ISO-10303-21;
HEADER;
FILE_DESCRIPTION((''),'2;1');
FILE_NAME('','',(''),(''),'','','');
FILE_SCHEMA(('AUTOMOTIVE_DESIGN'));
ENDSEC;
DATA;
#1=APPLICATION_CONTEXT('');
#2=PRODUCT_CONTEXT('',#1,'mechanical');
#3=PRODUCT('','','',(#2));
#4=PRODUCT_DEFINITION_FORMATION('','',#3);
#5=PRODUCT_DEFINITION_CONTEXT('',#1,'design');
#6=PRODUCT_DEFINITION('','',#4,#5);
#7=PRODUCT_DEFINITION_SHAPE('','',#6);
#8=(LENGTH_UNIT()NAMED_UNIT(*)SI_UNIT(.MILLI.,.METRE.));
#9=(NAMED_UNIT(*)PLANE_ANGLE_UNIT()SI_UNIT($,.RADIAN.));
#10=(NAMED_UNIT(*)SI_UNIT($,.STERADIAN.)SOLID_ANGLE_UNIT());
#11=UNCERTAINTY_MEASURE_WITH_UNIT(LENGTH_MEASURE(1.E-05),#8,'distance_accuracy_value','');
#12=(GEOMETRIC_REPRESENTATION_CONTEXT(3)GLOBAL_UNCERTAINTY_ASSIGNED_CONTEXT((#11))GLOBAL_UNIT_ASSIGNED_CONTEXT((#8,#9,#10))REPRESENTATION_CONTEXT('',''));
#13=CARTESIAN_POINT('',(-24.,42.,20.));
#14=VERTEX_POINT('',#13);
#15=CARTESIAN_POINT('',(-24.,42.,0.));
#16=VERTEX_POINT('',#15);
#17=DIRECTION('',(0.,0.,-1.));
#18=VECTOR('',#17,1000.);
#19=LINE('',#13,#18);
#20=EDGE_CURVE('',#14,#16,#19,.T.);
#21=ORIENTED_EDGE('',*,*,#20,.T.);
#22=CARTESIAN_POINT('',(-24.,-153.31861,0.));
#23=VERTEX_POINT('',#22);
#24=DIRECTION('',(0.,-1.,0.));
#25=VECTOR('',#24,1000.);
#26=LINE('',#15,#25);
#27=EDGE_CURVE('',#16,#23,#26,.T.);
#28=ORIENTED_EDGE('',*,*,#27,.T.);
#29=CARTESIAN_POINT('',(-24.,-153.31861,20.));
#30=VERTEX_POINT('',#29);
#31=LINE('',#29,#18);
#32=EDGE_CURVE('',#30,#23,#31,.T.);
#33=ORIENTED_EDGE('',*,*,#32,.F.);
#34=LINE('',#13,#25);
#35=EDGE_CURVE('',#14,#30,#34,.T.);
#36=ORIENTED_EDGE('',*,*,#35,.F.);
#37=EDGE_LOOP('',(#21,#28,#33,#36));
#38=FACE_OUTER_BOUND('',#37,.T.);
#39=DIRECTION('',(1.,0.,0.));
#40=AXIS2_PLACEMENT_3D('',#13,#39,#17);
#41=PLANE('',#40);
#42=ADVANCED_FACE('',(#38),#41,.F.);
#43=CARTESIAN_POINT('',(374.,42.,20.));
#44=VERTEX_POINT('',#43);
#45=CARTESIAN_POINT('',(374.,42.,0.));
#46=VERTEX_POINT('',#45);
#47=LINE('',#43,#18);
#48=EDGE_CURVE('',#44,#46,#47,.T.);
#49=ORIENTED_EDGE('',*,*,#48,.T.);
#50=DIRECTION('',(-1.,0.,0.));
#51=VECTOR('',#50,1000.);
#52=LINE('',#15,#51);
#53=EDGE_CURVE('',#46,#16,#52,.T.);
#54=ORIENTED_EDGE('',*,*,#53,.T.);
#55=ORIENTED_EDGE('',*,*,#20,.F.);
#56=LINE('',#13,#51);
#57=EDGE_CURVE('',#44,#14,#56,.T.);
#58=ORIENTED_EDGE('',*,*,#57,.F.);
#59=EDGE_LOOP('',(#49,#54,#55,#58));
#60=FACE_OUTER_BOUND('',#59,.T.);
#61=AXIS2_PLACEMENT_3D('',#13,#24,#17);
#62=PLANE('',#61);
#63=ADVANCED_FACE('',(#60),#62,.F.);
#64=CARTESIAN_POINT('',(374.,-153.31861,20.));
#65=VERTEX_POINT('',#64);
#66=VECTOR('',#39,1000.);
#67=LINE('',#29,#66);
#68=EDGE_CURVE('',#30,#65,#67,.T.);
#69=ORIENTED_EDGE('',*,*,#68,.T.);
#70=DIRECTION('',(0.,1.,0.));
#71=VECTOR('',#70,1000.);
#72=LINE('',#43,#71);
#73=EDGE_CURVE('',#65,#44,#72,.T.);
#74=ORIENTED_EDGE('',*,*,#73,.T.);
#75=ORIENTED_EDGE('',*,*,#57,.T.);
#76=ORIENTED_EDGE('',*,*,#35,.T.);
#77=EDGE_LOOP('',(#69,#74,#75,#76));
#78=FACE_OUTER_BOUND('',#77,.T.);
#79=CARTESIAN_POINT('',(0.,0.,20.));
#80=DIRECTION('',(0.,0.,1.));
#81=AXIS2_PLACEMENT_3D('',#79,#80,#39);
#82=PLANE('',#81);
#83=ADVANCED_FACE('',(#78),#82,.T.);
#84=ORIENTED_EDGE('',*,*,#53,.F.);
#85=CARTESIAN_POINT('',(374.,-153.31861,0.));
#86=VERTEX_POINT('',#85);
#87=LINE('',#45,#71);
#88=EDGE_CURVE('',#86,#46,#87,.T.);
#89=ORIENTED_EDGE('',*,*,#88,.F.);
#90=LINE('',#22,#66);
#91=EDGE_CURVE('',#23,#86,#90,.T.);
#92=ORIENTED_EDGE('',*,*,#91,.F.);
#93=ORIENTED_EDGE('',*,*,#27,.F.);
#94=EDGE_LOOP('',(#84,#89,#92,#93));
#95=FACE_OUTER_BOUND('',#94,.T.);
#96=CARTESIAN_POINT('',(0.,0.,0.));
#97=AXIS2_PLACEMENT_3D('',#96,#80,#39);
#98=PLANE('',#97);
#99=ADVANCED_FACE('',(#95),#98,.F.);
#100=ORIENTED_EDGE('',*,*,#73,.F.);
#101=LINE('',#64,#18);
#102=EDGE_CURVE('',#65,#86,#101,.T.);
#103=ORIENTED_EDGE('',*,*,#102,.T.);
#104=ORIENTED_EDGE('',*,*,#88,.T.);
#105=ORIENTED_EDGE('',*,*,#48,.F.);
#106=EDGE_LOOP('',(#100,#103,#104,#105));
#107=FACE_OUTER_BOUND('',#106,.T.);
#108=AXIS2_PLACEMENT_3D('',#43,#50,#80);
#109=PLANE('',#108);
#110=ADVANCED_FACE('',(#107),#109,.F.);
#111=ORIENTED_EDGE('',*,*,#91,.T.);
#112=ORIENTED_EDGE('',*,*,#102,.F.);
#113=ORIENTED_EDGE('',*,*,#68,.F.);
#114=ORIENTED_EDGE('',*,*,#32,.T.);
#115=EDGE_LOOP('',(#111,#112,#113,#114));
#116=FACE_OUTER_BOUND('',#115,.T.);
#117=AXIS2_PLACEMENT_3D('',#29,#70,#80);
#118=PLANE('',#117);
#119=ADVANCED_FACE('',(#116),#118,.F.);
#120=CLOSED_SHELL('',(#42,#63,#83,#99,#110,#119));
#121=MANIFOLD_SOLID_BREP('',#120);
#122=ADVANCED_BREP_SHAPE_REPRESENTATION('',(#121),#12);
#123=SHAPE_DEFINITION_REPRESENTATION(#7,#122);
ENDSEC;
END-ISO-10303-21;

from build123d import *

# Parameters (mm, degrees)
SKETCH_1_W      = 398
SKETCH_1_H      = 195.318610112
EXTRUDE_1_DEPTH = 20


with BuildPart() as part:
    # 草图1 → 凸台-拉伸1 (new body)
    with BuildSketch(Plane.XY):
        with Locations((175, -55.659305056)):
            Rectangle(SKETCH_1_W, SKETCH_1_H)
    extrude(amount=EXTRUDE_1_DEPTH)


solid = part.part
